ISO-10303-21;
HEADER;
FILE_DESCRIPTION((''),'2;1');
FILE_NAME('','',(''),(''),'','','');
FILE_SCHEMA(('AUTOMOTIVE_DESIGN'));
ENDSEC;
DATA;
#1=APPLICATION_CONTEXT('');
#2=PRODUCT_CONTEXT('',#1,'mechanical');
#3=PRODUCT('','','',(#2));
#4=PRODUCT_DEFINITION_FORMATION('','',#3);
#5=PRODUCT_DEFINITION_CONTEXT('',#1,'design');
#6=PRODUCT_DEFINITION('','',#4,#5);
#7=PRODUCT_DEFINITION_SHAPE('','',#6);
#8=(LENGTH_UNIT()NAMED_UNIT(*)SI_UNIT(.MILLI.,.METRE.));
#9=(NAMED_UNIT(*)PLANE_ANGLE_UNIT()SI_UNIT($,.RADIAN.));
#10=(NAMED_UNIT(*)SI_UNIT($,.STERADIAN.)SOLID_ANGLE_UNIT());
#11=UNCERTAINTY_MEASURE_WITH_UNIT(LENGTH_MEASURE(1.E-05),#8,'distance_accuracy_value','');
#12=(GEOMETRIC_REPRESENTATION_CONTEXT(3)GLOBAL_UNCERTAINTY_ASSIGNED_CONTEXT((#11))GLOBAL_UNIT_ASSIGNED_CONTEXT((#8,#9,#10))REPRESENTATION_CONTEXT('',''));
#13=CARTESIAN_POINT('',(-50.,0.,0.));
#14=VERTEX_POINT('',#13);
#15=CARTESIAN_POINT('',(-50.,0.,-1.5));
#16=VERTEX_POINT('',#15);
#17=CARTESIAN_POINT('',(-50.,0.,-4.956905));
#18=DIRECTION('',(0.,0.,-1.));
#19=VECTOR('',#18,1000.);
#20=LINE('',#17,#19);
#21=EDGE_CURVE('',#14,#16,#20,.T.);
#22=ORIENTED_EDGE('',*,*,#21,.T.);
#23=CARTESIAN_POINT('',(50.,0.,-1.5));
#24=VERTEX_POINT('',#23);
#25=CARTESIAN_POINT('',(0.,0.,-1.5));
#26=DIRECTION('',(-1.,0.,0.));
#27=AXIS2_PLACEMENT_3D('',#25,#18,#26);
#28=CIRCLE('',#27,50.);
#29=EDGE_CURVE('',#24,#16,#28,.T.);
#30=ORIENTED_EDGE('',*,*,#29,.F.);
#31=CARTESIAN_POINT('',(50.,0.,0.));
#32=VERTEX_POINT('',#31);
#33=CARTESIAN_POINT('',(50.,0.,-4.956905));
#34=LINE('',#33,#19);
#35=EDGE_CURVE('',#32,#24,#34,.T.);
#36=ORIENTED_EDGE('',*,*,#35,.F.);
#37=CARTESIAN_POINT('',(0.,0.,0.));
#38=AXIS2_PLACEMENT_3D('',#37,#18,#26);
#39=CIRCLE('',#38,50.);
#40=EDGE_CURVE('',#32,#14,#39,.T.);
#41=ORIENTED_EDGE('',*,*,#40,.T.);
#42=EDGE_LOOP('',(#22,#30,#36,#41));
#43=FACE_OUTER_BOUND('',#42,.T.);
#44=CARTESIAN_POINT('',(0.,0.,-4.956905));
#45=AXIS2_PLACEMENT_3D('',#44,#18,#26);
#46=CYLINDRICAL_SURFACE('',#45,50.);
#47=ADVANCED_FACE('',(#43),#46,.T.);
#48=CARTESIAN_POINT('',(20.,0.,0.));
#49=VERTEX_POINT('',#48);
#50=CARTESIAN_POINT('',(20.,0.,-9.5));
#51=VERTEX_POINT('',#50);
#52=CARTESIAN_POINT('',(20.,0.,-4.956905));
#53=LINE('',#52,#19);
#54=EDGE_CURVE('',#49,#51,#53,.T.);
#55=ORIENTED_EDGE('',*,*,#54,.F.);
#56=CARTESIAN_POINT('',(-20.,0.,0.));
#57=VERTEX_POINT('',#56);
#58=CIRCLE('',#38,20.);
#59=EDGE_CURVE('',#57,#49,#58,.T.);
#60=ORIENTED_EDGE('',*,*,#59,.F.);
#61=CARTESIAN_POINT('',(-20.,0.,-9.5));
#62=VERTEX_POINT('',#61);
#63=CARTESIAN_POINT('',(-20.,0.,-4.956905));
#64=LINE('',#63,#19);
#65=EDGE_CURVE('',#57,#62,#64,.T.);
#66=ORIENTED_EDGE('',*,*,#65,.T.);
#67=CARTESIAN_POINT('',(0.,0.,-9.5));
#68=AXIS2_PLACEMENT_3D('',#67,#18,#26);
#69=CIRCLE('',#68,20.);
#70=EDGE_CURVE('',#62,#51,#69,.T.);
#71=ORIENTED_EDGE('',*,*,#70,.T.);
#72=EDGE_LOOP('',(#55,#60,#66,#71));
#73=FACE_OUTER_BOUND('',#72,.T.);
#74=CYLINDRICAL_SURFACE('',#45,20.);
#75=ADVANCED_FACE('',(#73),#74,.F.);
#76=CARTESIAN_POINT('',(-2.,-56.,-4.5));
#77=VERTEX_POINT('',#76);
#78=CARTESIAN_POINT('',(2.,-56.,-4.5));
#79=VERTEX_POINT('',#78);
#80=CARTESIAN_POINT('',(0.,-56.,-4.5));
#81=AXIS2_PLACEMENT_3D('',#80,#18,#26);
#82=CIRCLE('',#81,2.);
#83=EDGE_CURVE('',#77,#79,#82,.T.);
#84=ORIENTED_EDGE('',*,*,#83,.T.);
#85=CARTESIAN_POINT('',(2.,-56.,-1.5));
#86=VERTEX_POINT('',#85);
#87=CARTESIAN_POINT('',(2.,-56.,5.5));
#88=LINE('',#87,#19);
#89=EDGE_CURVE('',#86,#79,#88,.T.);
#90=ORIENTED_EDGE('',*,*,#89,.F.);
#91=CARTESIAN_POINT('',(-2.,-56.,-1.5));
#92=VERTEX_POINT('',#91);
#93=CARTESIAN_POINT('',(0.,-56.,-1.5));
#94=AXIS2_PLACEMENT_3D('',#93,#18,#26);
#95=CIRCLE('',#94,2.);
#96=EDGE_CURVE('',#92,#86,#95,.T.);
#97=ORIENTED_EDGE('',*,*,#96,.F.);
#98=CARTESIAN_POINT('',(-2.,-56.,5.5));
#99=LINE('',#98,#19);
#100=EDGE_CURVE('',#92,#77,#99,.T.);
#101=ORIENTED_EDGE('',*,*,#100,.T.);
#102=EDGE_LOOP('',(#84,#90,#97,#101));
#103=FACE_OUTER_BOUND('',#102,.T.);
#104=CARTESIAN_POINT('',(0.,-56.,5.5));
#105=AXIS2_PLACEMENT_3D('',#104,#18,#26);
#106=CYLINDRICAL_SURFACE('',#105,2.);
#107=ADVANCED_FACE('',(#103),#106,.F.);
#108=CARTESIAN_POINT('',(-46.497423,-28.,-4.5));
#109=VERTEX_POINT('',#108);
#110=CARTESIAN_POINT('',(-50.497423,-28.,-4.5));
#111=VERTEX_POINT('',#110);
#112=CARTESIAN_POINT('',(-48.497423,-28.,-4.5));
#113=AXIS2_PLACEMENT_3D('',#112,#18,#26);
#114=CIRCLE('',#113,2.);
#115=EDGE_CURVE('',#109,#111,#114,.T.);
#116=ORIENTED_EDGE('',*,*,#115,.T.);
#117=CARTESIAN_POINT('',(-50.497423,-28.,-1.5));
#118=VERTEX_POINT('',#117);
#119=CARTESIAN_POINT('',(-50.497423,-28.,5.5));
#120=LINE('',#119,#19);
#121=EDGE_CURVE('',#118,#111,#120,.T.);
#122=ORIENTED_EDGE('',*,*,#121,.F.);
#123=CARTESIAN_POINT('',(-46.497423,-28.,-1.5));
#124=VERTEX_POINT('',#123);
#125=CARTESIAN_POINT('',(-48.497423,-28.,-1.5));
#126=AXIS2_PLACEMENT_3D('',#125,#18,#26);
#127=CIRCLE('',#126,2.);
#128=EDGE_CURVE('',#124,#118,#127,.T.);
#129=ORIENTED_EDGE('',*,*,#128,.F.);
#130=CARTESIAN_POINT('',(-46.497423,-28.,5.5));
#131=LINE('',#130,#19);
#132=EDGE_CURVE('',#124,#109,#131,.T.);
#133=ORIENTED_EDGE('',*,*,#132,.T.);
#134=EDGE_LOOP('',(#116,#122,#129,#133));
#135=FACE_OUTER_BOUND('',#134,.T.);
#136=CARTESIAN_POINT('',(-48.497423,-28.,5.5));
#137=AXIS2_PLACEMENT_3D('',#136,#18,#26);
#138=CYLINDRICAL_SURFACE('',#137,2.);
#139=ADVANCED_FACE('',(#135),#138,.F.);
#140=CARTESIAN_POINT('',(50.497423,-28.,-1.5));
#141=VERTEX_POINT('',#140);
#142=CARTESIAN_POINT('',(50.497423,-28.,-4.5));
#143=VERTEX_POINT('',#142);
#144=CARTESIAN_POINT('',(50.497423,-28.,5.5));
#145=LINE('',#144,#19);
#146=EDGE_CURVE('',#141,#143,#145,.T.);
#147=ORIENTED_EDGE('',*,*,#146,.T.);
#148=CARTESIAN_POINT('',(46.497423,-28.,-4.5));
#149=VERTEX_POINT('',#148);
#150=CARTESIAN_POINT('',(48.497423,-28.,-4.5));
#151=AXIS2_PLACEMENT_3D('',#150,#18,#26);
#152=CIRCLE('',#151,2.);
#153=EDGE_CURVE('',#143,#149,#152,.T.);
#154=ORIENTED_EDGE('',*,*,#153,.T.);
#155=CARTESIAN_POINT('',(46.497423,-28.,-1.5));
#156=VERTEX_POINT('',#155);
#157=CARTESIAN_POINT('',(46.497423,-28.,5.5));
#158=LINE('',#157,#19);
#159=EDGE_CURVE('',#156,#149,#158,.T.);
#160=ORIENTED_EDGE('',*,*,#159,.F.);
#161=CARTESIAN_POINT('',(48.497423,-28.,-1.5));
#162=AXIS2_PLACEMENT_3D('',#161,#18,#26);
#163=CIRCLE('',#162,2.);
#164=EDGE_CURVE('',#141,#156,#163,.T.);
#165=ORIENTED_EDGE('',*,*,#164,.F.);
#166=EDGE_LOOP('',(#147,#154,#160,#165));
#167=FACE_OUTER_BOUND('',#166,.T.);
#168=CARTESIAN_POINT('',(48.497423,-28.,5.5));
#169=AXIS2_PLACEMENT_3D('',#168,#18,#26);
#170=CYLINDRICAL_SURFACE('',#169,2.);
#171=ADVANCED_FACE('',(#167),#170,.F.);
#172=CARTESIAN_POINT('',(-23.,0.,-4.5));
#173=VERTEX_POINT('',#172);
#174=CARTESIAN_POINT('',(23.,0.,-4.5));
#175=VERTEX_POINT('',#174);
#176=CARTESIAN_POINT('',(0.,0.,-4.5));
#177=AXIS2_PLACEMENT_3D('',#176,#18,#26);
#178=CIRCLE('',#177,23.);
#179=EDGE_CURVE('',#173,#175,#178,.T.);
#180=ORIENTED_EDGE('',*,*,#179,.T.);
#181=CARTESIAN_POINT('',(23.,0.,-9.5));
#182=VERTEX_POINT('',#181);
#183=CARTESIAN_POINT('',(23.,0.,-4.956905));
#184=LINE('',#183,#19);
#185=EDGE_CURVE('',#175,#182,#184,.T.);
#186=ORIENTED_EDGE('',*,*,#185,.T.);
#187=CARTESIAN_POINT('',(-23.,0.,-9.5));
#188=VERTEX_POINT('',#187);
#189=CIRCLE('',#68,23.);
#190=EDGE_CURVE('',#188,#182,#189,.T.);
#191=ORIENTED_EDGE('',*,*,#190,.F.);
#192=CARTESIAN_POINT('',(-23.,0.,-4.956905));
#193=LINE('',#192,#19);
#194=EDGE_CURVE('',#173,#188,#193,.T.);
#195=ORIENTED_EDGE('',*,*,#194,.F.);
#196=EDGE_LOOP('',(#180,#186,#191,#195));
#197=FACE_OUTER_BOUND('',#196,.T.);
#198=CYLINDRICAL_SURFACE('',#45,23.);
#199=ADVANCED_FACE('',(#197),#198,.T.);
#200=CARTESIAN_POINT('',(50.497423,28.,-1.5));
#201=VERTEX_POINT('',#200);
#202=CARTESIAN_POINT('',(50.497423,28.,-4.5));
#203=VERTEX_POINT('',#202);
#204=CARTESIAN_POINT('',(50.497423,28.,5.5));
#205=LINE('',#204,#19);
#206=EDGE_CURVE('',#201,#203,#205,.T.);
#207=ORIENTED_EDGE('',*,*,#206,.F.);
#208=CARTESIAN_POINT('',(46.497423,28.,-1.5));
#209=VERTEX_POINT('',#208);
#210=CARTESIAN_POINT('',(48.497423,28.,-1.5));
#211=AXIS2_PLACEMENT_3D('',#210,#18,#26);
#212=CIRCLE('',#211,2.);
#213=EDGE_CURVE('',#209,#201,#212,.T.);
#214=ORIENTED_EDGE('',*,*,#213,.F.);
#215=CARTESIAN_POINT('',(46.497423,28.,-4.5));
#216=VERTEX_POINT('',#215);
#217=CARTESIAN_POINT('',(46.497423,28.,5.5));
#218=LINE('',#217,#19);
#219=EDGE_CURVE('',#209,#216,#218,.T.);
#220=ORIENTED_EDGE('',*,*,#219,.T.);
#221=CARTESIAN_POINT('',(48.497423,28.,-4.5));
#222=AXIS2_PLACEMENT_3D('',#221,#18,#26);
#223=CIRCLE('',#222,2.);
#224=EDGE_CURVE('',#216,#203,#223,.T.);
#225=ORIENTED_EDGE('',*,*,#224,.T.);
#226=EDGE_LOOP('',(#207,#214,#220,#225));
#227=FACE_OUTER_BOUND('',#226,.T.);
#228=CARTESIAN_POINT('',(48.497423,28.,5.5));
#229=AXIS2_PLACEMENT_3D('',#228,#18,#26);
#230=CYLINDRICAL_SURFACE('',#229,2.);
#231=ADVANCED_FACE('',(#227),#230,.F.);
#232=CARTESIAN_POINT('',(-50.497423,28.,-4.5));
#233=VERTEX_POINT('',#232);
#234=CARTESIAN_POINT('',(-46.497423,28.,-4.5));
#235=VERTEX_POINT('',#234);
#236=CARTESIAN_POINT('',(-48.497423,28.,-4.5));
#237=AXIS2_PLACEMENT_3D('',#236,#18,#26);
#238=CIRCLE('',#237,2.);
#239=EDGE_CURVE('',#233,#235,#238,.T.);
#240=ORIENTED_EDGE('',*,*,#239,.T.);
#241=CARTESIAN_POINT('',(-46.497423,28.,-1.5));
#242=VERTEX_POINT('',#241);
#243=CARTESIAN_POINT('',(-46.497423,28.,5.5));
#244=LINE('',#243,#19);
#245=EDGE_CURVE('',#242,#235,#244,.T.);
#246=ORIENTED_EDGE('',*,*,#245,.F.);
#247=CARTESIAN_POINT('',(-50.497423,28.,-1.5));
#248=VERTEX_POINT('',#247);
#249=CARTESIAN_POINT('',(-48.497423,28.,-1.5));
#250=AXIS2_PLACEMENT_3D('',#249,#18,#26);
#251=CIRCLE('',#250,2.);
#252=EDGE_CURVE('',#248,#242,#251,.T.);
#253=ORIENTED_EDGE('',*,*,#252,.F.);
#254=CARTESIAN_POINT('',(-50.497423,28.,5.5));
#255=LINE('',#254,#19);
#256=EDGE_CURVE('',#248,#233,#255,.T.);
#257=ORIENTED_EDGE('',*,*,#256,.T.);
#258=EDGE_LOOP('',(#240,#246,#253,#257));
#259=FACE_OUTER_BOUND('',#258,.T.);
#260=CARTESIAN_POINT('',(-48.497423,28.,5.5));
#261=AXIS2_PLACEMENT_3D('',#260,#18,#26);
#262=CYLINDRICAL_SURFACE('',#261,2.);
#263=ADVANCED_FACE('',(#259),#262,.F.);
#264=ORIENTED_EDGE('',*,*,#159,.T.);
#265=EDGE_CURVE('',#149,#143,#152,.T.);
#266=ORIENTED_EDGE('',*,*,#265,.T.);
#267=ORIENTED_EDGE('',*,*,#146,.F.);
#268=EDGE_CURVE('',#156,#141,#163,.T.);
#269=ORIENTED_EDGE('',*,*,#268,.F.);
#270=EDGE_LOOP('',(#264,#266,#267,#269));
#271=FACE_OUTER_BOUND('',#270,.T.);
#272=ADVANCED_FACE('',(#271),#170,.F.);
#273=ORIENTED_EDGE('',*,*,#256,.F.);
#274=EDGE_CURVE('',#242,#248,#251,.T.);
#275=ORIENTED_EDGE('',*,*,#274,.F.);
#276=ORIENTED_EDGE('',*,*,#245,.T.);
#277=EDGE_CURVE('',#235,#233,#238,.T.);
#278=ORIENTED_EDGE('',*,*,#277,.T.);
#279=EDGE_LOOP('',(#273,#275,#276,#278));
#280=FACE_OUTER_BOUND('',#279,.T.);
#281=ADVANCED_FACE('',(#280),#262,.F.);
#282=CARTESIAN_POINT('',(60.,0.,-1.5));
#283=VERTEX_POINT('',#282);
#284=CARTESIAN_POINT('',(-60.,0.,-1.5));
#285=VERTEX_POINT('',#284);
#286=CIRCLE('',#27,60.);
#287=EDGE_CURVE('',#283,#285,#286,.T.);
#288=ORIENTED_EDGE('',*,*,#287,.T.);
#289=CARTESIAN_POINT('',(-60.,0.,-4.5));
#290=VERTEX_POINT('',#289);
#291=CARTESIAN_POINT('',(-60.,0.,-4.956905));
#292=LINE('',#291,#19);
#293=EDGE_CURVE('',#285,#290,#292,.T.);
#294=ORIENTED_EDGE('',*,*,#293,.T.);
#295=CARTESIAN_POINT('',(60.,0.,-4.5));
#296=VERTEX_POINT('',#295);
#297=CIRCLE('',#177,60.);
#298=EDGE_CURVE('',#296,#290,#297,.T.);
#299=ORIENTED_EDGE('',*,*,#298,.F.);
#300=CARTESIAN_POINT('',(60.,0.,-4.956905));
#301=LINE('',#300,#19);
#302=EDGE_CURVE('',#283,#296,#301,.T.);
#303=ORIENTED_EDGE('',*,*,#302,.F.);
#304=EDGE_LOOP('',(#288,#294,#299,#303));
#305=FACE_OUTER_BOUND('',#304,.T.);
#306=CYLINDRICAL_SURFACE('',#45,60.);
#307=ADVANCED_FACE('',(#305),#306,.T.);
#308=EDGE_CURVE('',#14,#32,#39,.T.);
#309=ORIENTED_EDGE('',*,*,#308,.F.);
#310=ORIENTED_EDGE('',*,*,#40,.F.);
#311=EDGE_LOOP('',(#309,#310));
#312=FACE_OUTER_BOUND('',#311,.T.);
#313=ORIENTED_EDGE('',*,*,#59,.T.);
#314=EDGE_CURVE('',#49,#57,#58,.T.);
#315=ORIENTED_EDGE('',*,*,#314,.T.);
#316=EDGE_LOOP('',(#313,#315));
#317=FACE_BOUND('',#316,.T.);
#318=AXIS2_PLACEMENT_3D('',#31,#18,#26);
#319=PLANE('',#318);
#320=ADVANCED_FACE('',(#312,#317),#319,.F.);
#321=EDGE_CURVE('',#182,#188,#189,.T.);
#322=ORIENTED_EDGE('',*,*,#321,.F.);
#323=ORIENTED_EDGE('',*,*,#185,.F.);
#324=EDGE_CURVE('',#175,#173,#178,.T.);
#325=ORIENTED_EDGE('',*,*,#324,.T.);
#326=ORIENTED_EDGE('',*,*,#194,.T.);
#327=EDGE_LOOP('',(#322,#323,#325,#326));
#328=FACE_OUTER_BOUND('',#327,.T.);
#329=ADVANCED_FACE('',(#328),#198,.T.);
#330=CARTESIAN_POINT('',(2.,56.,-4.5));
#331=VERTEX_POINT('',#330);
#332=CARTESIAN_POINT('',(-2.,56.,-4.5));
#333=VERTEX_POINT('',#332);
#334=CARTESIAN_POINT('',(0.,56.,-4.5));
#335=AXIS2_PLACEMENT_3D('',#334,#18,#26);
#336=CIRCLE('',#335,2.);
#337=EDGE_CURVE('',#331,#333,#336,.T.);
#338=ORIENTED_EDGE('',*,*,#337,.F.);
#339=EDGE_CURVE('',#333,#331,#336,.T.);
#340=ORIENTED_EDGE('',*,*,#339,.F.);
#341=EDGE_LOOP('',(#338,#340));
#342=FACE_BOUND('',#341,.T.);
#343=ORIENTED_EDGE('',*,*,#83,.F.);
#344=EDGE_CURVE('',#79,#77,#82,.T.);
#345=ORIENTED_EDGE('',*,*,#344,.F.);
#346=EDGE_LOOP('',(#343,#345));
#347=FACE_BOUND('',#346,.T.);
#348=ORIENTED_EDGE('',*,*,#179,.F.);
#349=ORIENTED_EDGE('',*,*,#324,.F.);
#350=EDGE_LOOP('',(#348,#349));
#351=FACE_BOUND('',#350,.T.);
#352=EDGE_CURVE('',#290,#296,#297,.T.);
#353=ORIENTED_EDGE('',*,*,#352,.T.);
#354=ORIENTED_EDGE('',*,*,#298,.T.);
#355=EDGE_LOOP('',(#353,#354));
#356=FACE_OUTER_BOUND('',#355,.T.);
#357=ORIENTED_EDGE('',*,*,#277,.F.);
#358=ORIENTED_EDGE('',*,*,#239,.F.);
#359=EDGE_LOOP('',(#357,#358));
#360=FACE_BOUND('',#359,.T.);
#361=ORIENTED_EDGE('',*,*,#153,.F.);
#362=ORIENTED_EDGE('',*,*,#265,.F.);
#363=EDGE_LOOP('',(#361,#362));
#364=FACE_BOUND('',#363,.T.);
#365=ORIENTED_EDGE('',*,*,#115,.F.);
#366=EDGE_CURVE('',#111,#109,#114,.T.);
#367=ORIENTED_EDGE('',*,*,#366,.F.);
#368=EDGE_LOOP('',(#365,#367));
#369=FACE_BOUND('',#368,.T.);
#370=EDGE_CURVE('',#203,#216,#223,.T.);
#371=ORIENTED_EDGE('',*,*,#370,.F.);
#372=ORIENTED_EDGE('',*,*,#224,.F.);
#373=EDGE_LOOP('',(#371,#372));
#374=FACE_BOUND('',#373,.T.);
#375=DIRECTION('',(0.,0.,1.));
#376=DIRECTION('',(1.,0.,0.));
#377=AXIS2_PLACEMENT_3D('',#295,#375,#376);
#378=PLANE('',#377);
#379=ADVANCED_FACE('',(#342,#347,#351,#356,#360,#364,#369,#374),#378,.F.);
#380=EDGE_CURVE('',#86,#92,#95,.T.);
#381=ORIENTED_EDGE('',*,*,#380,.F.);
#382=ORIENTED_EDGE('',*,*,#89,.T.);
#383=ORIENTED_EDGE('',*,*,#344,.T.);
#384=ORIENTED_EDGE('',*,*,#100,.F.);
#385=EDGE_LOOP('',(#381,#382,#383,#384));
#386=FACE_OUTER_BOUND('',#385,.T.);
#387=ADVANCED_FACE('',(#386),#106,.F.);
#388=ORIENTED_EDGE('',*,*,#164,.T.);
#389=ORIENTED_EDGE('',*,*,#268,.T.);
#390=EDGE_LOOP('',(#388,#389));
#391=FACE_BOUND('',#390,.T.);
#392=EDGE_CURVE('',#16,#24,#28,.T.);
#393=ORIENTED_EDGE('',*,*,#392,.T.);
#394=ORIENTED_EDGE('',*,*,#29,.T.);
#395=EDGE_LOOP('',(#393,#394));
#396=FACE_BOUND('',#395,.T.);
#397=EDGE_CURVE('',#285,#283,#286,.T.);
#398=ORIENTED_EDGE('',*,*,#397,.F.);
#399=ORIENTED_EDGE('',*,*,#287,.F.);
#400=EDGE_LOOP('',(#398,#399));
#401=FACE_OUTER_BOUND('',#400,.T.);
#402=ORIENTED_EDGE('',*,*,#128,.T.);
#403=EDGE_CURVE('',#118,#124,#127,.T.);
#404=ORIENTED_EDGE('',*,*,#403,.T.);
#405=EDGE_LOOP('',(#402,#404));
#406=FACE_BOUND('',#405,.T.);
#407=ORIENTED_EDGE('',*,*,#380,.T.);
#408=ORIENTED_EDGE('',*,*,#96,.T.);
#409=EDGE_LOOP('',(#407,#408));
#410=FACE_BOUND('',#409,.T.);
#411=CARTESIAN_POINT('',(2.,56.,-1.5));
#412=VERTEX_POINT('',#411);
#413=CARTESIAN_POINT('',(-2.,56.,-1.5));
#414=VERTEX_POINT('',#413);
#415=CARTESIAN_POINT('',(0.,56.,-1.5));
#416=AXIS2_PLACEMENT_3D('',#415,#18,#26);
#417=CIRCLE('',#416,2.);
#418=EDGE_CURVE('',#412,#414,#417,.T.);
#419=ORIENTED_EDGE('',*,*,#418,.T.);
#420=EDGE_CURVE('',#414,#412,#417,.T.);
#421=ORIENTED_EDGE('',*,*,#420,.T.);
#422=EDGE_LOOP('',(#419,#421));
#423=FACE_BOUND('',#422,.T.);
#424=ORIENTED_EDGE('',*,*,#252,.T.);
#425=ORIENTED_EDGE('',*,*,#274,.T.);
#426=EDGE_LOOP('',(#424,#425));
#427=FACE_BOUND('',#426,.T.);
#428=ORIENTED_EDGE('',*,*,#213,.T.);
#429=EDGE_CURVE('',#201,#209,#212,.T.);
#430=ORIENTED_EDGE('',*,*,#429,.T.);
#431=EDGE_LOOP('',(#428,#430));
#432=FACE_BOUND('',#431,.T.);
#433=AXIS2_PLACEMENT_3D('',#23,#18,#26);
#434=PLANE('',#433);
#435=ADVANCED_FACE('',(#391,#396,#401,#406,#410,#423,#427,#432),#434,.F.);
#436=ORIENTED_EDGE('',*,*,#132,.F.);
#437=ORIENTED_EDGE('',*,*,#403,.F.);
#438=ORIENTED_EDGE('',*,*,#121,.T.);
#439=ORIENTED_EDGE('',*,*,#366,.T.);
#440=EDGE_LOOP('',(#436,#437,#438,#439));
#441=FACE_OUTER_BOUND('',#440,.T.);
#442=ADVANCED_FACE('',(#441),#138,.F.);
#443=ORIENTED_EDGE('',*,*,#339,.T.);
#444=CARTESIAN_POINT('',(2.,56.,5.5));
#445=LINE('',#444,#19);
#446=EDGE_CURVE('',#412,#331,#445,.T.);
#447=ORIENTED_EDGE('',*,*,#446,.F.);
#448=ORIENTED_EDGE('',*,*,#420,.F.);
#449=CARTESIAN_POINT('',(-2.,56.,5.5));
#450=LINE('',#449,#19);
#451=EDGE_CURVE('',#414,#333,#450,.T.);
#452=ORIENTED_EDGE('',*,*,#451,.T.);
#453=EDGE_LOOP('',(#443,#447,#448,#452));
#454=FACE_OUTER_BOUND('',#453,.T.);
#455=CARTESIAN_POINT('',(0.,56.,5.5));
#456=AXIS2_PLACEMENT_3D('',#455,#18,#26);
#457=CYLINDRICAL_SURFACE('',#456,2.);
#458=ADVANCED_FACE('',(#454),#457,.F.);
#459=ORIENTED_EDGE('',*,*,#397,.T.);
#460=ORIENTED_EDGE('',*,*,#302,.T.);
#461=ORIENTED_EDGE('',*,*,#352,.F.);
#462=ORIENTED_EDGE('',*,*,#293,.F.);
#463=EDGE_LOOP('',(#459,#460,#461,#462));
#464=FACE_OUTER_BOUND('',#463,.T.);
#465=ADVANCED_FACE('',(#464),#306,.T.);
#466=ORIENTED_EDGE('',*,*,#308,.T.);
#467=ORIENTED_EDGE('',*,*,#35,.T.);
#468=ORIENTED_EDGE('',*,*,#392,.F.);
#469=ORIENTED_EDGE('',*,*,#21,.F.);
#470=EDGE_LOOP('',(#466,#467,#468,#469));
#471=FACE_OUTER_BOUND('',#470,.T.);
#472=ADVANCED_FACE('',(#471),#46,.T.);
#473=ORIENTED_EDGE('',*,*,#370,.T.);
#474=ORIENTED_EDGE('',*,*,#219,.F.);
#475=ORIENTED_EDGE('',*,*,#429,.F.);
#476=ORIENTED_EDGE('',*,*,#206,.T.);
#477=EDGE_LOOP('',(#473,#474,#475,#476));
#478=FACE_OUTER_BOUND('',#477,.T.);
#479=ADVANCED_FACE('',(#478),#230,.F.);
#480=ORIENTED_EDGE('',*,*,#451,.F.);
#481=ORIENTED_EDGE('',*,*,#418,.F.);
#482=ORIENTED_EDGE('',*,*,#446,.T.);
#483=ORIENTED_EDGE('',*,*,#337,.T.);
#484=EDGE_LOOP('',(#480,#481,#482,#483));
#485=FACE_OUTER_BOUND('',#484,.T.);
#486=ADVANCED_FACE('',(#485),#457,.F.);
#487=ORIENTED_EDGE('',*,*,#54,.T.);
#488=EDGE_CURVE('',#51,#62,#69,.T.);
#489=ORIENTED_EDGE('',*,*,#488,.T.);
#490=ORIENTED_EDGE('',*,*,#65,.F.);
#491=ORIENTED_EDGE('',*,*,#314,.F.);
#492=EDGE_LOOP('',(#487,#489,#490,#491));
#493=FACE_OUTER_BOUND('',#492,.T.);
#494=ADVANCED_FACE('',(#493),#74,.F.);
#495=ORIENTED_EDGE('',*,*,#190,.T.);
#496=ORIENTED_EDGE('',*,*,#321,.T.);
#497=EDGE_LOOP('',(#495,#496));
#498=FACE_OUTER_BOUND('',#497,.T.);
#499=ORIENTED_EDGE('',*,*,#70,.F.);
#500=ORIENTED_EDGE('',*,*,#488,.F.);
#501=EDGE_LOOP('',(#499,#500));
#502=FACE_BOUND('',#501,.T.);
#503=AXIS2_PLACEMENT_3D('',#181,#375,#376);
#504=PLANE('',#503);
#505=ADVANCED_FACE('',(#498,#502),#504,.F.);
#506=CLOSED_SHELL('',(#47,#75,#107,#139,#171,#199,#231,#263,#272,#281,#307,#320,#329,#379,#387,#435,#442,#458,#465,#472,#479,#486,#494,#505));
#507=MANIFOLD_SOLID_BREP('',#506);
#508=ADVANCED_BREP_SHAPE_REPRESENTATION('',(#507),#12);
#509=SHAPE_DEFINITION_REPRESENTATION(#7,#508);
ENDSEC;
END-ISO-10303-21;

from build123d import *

# Parameters (mm, degrees)
SKETCH2_R          = 2
CUT_EXTRUDE1_DEPTH = 10


with BuildPart() as part:
    # Sketch1 → Revolve1 (revolve)
    with BuildSketch(Plane(origin=(0, 0, 0), x_dir=(1, 0, 0), z_dir=(0, 1, 0)), mode=Mode.PRIVATE) as revolve1_sk:
        Polygon((20, 9.5), (20, 0), (50, 0), (50, 1.5), (60, 1.5), (60, 4.5), (23, 4.5), (23, 9.5), align=None)
    revolve(revolve1_sk.sketch.rotate(Axis((0, 0, -4.956904689), (0, 0, 1)), 180), axis=Axis((0, 0, -4.956904689), (0, 0, 1)))

    # Sketch2 → Cut-Extrude1 (cut)
    with BuildSketch(Plane(origin=(0, 0, -4.5), x_dir=(-1, 0, 0), z_dir=(0, 0, -1))):
        with Locations((0, 56)):
            Circle(SKETCH2_R)
        with Locations((-48.497422612, 28)):
            Circle(SKETCH2_R)
        with Locations((-48.497422612, -28)):
            Circle(SKETCH2_R)
        with Locations((0, -56)):
            Circle(SKETCH2_R)
        with Locations((48.497422612, -28)):
            Circle(SKETCH2_R)
        with Locations((48.497422612, 28)):
            Circle(SKETCH2_R)
    extrude(amount=-CUT_EXTRUDE1_DEPTH, mode=Mode.SUBTRACT)


solid = part.part
